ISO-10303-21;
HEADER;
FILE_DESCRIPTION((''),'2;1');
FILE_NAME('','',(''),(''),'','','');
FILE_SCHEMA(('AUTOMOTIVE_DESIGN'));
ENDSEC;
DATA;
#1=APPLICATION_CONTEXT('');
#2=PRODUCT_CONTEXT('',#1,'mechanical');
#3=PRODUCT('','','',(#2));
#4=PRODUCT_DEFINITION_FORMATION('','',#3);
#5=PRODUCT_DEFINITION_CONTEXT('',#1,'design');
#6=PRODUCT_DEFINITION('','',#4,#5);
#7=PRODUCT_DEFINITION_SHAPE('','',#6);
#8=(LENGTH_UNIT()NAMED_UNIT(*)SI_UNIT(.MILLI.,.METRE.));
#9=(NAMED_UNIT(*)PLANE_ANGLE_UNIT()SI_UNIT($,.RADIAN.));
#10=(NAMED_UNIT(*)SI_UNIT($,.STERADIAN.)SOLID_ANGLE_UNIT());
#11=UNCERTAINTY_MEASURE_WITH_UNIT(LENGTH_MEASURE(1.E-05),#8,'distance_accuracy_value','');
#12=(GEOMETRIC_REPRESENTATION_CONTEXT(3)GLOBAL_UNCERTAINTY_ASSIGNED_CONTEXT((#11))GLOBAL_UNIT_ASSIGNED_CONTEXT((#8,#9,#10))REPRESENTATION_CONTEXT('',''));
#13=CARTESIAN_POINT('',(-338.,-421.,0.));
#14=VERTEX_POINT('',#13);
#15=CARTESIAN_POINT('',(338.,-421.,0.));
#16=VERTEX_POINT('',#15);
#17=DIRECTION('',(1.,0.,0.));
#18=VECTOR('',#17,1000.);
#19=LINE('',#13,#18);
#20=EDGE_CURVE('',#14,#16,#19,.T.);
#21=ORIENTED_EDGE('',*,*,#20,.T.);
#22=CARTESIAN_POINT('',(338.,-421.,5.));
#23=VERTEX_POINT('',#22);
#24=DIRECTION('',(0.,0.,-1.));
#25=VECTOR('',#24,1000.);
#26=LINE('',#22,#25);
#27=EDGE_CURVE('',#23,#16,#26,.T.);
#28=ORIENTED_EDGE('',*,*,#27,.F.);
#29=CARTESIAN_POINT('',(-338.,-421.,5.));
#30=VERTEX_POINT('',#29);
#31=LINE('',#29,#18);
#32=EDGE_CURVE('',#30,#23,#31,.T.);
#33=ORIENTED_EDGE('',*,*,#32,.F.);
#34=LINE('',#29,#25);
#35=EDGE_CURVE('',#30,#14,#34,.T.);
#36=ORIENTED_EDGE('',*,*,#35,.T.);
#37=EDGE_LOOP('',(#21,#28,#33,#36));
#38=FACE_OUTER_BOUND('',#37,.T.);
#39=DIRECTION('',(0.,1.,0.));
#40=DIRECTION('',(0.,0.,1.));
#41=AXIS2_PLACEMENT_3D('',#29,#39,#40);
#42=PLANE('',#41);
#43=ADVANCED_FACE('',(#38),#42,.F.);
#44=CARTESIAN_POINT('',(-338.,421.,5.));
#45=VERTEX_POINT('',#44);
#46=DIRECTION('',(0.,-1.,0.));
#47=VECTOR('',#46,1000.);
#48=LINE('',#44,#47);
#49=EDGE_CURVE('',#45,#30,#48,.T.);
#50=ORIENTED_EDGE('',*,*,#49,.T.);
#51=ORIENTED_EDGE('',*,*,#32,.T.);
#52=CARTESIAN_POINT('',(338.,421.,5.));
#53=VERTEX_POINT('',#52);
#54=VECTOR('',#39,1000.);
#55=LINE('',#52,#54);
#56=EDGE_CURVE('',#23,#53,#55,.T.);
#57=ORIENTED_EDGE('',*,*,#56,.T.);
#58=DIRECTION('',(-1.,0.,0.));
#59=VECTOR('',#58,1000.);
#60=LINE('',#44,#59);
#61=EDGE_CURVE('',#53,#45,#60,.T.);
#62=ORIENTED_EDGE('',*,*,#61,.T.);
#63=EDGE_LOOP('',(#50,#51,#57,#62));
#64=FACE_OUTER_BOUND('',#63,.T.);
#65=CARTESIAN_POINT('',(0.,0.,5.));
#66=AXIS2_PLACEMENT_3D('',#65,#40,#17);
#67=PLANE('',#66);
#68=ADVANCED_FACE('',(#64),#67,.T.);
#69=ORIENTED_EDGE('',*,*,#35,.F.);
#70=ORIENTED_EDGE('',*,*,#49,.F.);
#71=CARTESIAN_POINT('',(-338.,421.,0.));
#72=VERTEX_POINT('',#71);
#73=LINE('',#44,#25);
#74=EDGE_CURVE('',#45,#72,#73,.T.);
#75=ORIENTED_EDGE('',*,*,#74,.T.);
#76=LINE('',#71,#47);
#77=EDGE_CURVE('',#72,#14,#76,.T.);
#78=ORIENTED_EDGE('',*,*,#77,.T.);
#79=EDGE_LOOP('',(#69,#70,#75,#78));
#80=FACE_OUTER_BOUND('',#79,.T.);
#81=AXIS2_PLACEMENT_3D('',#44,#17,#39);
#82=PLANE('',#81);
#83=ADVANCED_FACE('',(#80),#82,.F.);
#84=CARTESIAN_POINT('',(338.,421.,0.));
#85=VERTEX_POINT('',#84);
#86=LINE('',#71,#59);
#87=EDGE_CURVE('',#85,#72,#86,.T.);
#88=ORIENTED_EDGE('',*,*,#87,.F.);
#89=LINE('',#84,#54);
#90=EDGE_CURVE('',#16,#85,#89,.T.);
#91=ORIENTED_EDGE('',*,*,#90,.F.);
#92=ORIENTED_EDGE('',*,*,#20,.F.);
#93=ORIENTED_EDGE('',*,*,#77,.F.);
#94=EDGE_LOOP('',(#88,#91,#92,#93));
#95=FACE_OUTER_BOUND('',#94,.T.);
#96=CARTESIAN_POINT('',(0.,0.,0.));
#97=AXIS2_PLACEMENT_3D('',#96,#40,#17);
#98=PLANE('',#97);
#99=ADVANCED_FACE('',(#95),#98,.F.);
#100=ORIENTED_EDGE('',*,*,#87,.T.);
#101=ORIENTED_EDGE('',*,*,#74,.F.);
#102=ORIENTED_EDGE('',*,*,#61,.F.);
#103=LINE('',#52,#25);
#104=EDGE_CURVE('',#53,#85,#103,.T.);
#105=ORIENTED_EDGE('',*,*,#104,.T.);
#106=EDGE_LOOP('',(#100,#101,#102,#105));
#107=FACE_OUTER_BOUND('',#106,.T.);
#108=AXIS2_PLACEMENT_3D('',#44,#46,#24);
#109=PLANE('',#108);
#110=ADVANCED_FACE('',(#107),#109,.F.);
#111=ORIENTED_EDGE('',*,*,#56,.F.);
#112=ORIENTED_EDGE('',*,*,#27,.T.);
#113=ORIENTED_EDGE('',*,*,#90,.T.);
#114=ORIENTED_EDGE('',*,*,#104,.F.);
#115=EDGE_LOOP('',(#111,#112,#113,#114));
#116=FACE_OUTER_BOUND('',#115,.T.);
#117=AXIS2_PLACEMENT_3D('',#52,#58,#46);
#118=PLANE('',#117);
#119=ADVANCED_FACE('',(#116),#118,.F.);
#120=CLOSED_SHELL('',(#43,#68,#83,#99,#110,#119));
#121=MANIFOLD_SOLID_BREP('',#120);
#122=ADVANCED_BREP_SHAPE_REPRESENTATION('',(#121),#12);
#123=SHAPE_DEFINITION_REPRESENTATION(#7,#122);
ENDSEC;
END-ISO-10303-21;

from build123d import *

# Parameters (mm, degrees)
SKETCH_1_W      = 676
SKETCH_1_H      = 842
EXTRUDE_1_DEPTH = 5


with BuildPart() as part:
    # 草图1 → 凸台-拉伸1 (new body)
    with BuildSketch(Plane.XY):
        Rectangle(SKETCH_1_W, SKETCH_1_H)
    extrude(amount=EXTRUDE_1_DEPTH)


solid = part.part
